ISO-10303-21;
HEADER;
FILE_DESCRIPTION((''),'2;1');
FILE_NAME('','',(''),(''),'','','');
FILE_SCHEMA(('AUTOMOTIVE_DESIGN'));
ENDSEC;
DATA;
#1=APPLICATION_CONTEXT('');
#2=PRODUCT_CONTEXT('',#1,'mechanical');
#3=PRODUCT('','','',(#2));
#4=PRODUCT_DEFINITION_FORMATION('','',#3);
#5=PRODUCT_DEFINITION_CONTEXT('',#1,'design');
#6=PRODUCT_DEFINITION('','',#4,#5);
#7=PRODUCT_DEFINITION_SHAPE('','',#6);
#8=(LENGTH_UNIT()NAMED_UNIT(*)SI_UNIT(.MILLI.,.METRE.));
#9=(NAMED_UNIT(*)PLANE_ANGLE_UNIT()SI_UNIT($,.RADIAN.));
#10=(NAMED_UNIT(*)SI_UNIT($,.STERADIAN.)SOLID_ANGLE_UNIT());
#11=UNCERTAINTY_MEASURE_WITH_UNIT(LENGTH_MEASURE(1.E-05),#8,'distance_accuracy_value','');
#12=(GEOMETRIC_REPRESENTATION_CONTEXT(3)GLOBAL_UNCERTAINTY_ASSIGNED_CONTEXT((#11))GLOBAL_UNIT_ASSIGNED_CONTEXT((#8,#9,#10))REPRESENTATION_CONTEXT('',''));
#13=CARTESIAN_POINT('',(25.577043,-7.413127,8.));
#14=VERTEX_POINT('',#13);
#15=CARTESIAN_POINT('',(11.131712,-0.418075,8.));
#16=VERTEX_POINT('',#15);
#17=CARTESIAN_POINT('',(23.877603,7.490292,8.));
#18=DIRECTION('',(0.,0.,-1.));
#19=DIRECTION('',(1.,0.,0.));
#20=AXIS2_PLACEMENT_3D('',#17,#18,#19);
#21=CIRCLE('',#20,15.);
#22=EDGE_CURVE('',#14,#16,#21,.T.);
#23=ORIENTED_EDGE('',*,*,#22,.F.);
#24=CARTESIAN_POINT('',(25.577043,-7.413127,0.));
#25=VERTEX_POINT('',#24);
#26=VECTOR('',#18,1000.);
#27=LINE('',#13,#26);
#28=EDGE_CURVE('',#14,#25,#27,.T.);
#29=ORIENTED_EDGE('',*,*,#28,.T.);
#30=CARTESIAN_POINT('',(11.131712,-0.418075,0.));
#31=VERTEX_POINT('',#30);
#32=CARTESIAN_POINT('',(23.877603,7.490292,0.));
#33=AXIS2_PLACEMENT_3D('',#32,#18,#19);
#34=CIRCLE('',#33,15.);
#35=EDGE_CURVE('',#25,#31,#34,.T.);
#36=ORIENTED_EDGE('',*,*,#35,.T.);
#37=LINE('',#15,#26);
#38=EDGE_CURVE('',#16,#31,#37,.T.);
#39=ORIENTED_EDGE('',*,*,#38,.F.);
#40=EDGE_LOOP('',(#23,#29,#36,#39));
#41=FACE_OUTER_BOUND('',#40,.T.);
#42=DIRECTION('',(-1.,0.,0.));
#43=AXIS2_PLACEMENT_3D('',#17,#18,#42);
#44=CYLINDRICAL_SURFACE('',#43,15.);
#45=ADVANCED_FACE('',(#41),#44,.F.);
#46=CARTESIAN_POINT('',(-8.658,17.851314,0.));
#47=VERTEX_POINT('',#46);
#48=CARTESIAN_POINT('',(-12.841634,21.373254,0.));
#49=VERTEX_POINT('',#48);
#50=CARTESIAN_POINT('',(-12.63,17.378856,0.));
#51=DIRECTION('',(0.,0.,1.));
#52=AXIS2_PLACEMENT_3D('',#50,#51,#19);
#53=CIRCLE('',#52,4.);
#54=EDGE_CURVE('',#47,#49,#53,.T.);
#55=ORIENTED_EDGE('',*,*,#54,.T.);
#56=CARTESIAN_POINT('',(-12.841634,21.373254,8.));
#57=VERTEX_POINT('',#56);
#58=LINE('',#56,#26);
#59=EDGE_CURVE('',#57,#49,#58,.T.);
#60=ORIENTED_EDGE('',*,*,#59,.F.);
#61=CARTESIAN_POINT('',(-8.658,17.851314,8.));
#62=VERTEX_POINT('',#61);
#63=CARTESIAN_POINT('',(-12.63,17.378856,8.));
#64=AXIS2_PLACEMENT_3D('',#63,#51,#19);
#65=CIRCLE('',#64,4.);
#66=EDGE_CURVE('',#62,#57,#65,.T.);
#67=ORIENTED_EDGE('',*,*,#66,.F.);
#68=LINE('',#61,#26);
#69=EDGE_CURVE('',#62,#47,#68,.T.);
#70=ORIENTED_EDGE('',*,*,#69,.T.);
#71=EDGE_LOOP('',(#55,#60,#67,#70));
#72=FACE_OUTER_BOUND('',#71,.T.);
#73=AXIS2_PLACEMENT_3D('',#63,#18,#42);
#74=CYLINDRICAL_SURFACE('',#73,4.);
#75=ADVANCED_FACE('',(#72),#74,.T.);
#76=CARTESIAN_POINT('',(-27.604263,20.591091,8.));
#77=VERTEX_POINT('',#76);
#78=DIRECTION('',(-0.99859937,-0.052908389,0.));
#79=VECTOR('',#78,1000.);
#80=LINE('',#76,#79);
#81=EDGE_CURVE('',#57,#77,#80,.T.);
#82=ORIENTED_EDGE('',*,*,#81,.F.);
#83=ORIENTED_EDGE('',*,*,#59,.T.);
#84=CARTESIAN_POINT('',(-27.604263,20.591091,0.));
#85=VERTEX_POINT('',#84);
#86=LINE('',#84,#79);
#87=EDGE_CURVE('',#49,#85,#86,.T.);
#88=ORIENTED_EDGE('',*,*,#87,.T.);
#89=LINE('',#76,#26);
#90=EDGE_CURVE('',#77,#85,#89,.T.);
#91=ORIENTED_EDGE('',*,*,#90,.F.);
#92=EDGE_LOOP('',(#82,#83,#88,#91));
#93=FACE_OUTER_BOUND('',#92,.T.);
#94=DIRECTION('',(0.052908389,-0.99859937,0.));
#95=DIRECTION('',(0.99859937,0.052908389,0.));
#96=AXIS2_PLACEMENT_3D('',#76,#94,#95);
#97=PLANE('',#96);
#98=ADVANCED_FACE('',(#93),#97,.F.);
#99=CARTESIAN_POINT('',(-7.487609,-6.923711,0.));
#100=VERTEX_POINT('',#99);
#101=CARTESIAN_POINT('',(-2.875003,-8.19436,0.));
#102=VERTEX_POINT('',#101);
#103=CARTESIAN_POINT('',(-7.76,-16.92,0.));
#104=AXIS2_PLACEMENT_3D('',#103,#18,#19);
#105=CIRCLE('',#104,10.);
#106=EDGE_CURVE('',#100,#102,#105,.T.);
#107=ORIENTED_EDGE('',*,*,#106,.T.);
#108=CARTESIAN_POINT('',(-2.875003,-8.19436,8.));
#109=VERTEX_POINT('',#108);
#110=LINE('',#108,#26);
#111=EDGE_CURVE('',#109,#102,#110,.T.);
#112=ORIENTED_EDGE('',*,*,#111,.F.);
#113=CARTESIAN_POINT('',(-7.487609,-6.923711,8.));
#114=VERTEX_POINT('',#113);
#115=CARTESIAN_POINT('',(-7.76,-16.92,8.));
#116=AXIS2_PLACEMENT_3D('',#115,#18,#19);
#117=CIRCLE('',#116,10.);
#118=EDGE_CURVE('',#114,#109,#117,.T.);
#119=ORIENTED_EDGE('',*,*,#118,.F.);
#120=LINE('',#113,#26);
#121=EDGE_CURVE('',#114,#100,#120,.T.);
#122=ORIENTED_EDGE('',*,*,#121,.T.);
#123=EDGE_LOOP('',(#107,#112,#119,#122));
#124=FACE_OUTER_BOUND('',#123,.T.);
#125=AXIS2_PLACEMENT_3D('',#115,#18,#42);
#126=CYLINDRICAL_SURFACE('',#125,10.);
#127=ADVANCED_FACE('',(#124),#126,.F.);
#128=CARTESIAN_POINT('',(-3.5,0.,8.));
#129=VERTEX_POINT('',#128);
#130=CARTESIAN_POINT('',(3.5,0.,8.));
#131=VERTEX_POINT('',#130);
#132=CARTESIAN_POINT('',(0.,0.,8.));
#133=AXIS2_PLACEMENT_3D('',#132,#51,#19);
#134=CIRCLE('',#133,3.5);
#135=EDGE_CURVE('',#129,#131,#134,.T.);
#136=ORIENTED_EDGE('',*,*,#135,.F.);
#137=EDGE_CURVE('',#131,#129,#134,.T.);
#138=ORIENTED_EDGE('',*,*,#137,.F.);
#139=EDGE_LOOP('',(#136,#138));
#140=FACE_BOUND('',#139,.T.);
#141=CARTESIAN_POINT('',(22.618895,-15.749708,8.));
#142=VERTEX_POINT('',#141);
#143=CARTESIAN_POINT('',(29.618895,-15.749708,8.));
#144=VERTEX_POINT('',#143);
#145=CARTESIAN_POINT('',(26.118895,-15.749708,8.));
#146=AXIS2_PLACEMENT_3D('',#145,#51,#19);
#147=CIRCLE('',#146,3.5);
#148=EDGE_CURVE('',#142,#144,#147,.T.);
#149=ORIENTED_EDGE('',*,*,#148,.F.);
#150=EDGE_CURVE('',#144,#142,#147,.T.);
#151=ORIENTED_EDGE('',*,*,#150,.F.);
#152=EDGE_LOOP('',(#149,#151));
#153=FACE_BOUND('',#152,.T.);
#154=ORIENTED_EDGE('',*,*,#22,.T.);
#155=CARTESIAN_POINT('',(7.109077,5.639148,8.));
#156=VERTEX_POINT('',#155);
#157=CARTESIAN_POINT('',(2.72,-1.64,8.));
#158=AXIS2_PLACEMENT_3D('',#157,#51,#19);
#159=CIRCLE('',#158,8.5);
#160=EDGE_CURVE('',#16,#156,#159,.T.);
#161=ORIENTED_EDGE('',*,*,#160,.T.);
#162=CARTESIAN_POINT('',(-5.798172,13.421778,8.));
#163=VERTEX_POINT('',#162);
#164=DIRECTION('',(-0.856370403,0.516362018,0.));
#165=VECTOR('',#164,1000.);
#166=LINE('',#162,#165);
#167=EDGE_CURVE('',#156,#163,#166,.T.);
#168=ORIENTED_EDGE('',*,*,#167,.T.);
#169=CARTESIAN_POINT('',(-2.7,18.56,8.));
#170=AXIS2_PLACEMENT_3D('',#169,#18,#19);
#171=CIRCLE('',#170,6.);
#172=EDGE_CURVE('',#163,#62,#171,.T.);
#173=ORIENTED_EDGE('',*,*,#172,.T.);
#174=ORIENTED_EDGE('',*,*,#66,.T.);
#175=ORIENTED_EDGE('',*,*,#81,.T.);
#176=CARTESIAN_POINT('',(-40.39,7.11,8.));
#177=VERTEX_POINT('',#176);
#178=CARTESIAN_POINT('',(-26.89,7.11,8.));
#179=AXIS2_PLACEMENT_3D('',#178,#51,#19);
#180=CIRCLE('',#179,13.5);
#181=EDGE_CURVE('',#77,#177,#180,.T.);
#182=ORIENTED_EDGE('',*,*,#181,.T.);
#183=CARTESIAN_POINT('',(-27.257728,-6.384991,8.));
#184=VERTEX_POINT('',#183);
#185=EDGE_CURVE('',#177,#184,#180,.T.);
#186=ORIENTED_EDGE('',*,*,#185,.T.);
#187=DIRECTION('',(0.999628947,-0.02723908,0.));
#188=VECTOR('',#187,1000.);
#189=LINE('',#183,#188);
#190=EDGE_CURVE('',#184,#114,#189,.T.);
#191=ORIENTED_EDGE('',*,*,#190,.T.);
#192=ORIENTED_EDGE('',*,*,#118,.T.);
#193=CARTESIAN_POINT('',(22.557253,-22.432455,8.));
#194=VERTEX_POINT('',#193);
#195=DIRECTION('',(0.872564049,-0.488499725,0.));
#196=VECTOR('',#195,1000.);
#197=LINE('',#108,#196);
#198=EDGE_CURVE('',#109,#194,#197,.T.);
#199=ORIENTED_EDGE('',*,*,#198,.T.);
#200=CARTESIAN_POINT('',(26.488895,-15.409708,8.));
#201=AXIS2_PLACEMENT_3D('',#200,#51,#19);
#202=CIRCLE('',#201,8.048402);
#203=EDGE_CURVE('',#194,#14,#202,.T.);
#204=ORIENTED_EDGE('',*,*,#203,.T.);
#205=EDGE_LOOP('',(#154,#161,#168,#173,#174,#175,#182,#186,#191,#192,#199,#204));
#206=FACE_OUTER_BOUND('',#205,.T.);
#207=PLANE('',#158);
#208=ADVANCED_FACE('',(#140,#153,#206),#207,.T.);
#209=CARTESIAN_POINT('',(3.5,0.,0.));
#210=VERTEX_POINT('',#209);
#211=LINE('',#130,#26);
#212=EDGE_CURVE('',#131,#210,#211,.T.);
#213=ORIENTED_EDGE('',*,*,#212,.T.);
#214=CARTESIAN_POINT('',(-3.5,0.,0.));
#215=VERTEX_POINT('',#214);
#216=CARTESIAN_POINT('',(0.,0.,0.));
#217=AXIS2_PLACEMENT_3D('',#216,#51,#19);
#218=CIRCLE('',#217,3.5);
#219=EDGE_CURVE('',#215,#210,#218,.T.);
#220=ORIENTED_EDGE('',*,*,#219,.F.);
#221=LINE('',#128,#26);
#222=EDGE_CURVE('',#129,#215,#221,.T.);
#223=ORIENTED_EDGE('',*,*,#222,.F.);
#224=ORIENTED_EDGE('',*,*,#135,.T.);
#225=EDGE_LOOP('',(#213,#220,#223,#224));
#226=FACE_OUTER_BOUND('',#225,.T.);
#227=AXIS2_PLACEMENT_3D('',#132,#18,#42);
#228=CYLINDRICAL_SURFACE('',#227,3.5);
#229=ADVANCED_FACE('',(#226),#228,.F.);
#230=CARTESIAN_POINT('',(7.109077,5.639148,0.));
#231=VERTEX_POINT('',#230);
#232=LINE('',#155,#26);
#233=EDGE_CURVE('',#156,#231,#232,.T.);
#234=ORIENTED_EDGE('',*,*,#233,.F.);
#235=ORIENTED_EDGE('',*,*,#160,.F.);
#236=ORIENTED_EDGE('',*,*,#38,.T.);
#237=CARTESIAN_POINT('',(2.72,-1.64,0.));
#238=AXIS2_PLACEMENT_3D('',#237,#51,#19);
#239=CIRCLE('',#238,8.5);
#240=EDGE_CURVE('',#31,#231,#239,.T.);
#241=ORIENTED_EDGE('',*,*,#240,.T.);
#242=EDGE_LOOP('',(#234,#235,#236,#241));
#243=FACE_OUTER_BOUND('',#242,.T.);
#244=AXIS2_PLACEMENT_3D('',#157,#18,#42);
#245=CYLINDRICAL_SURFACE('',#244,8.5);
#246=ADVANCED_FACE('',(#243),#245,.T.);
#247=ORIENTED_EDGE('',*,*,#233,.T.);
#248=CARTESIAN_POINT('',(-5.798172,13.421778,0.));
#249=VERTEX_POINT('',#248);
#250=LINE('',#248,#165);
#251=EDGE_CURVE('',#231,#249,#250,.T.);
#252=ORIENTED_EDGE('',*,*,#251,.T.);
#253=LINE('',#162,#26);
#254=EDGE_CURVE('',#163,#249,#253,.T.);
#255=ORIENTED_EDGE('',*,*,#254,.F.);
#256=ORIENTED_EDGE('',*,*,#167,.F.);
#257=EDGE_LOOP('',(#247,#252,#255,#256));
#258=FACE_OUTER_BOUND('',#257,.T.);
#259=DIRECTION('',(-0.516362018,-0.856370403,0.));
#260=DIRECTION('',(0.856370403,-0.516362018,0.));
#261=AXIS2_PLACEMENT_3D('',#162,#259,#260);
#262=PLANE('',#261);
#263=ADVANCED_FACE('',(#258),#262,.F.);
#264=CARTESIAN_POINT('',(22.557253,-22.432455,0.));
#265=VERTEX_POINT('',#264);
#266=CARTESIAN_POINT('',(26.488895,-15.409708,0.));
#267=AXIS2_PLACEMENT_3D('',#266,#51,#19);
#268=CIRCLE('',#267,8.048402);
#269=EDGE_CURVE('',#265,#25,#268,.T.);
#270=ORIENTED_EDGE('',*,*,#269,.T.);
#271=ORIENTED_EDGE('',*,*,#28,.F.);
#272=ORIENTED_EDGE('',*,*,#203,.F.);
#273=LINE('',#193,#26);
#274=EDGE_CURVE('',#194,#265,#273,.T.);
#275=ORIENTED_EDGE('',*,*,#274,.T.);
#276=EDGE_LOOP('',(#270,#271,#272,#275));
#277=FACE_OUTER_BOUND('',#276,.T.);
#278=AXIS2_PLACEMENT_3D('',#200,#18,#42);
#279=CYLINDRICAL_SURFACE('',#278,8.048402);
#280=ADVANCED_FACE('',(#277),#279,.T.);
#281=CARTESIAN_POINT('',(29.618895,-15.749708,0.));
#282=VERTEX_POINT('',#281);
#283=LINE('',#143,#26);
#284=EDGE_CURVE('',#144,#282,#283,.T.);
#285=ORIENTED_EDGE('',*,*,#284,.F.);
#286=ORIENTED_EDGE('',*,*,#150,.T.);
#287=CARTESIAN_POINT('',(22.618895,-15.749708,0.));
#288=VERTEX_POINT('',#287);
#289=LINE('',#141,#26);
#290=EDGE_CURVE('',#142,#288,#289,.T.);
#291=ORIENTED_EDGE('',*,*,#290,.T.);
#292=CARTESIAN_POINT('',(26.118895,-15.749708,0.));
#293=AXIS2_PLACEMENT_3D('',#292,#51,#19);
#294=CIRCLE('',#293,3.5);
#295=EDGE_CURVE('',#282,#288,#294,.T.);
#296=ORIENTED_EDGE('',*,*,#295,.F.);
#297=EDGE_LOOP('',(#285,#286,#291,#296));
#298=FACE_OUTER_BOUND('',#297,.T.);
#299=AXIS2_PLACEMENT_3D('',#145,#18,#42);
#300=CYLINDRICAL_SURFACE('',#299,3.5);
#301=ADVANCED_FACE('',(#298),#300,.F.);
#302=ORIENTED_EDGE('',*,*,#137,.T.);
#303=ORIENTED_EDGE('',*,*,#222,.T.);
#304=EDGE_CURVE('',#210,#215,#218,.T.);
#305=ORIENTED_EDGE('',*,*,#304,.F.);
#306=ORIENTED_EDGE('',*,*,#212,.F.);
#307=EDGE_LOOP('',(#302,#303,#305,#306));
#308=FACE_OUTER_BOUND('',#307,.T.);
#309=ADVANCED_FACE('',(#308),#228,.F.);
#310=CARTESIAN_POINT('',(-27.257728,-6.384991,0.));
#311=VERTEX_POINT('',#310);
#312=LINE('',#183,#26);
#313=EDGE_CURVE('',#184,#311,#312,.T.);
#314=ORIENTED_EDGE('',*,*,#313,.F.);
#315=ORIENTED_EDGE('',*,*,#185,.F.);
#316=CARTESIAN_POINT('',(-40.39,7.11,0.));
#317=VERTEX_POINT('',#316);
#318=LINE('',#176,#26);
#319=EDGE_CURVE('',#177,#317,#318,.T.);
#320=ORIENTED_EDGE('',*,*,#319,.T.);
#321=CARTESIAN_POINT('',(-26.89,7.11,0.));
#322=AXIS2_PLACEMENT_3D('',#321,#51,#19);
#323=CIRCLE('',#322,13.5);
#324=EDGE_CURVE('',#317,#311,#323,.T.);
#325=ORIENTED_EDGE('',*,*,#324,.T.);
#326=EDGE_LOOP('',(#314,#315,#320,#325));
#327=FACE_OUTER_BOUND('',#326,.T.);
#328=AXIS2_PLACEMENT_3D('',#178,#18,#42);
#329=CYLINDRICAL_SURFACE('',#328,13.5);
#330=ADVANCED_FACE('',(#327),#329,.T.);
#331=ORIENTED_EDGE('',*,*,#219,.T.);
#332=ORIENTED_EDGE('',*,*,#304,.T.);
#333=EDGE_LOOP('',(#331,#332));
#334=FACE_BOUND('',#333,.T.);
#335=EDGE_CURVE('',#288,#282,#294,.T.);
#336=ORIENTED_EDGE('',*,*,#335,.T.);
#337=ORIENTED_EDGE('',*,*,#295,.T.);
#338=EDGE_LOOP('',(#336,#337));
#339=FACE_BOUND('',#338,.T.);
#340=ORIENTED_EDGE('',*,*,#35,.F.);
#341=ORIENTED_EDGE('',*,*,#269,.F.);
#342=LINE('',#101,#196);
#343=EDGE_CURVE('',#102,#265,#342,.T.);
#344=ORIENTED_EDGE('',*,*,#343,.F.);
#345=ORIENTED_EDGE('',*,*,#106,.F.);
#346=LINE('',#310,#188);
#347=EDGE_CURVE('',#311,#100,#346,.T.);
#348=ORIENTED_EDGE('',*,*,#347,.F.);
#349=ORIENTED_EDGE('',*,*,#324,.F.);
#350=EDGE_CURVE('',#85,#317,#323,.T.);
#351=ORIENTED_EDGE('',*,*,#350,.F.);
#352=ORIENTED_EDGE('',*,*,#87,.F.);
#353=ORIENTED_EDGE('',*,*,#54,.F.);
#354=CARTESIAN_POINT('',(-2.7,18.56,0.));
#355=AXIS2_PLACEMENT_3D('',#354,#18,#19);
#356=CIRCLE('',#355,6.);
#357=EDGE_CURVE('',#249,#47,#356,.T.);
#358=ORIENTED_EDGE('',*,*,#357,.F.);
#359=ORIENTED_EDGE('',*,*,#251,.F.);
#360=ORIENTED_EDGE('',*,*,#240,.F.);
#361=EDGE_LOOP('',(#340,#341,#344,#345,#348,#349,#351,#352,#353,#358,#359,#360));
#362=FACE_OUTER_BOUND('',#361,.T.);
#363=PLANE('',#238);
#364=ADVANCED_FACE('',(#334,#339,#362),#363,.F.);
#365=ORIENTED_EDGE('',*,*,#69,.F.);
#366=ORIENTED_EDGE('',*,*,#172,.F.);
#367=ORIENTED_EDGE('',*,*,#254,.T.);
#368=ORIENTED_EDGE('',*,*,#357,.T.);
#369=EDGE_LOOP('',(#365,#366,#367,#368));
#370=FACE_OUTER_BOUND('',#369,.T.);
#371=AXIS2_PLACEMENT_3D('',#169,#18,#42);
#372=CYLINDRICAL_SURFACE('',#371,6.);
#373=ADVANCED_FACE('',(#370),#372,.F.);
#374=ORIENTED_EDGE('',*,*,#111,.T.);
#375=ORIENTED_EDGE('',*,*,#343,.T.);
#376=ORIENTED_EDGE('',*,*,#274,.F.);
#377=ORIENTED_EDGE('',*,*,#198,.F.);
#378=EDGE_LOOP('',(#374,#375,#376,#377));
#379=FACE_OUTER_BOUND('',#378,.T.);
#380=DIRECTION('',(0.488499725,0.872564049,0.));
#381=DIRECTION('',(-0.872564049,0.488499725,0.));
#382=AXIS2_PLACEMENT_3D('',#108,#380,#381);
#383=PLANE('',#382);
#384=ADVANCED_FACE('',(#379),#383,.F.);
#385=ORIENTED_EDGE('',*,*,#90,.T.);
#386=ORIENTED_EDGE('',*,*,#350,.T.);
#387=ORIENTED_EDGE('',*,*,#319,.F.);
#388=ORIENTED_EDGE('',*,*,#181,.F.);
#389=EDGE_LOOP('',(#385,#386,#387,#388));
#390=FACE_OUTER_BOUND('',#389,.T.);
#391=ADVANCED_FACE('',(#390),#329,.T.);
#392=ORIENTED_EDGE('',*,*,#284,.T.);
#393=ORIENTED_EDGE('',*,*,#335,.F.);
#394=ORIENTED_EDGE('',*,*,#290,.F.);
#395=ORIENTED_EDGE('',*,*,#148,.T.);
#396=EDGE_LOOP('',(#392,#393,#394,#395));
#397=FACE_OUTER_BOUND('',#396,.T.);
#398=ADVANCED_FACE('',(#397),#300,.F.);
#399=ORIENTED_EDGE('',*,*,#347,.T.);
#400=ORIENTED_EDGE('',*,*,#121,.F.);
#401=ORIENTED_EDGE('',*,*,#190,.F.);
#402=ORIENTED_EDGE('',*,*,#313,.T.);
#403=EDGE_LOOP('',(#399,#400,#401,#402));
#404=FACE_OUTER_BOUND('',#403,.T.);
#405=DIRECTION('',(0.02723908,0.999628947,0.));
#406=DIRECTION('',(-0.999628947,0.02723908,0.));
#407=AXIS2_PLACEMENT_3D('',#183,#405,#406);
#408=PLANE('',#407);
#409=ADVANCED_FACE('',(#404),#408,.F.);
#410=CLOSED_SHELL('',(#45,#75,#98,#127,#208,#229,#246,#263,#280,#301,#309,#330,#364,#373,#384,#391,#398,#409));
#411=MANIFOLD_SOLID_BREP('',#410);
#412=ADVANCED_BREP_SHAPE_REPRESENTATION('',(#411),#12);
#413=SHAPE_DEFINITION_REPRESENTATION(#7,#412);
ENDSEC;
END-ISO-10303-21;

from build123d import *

# Parameters (mm, degrees)
SKETCH1_R           = 3.5
BOSS_EXTRUDE1_DEPTH = 8


with BuildPart() as part:
    # Sketch1 → Boss-Extrude1 (new body)
    with BuildSketch(Plane.XY):
        with BuildLine():
            Line((-5.798172106, 13.421777583), (7.10907715, 5.639148423))
            ThreePointArc((7.10907715, 5.639148423), (9.80078667, 3.06238877), (11.131712033, -0.418075011))
            ThreePointArc((11.131712033, -0.418075011), (17.340118207, -6.010126453), (25.57704331, -7.41312731))
            ThreePointArc((25.57704331, -7.41312731), (34.379390092, -16.99617332), (22.557253019, -22.432454651))
            Line((22.557253019, -22.432454651), (-2.875002754, -8.194359513))
            ThreePointArc((-2.875002754, -8.194359513), (-5.104195022, -7.279113116), (-7.487609197, -6.923710526))
            Line((-7.487609197, -6.923710526), (-27.257727584, -6.38499079))
            ThreePointArc((-27.257727584, -6.38499079), (-40.388886249, 6.936592853), (-27.604263246, 20.591091499))
            Line((-27.604263246, 20.591091499), (-12.841633554, 21.373253968))
            ThreePointArc((-12.841633554, 21.373253968), (-10.053936254, 20.438904782), (-8.658, 17.851313892))
            ThreePointArc((-8.658, 17.851313892), (-7.740710394, 15.305581662), (-5.798172106, 13.421777583))
        make_face()
        Circle(SKETCH1_R, mode=Mode.SUBTRACT)
        with Locations((26.118895321, -15.749708163)):
            Circle(SKETCH1_R, mode=Mode.SUBTRACT)
    extrude(amount=BOSS_EXTRUDE1_DEPTH)


solid = part.part
